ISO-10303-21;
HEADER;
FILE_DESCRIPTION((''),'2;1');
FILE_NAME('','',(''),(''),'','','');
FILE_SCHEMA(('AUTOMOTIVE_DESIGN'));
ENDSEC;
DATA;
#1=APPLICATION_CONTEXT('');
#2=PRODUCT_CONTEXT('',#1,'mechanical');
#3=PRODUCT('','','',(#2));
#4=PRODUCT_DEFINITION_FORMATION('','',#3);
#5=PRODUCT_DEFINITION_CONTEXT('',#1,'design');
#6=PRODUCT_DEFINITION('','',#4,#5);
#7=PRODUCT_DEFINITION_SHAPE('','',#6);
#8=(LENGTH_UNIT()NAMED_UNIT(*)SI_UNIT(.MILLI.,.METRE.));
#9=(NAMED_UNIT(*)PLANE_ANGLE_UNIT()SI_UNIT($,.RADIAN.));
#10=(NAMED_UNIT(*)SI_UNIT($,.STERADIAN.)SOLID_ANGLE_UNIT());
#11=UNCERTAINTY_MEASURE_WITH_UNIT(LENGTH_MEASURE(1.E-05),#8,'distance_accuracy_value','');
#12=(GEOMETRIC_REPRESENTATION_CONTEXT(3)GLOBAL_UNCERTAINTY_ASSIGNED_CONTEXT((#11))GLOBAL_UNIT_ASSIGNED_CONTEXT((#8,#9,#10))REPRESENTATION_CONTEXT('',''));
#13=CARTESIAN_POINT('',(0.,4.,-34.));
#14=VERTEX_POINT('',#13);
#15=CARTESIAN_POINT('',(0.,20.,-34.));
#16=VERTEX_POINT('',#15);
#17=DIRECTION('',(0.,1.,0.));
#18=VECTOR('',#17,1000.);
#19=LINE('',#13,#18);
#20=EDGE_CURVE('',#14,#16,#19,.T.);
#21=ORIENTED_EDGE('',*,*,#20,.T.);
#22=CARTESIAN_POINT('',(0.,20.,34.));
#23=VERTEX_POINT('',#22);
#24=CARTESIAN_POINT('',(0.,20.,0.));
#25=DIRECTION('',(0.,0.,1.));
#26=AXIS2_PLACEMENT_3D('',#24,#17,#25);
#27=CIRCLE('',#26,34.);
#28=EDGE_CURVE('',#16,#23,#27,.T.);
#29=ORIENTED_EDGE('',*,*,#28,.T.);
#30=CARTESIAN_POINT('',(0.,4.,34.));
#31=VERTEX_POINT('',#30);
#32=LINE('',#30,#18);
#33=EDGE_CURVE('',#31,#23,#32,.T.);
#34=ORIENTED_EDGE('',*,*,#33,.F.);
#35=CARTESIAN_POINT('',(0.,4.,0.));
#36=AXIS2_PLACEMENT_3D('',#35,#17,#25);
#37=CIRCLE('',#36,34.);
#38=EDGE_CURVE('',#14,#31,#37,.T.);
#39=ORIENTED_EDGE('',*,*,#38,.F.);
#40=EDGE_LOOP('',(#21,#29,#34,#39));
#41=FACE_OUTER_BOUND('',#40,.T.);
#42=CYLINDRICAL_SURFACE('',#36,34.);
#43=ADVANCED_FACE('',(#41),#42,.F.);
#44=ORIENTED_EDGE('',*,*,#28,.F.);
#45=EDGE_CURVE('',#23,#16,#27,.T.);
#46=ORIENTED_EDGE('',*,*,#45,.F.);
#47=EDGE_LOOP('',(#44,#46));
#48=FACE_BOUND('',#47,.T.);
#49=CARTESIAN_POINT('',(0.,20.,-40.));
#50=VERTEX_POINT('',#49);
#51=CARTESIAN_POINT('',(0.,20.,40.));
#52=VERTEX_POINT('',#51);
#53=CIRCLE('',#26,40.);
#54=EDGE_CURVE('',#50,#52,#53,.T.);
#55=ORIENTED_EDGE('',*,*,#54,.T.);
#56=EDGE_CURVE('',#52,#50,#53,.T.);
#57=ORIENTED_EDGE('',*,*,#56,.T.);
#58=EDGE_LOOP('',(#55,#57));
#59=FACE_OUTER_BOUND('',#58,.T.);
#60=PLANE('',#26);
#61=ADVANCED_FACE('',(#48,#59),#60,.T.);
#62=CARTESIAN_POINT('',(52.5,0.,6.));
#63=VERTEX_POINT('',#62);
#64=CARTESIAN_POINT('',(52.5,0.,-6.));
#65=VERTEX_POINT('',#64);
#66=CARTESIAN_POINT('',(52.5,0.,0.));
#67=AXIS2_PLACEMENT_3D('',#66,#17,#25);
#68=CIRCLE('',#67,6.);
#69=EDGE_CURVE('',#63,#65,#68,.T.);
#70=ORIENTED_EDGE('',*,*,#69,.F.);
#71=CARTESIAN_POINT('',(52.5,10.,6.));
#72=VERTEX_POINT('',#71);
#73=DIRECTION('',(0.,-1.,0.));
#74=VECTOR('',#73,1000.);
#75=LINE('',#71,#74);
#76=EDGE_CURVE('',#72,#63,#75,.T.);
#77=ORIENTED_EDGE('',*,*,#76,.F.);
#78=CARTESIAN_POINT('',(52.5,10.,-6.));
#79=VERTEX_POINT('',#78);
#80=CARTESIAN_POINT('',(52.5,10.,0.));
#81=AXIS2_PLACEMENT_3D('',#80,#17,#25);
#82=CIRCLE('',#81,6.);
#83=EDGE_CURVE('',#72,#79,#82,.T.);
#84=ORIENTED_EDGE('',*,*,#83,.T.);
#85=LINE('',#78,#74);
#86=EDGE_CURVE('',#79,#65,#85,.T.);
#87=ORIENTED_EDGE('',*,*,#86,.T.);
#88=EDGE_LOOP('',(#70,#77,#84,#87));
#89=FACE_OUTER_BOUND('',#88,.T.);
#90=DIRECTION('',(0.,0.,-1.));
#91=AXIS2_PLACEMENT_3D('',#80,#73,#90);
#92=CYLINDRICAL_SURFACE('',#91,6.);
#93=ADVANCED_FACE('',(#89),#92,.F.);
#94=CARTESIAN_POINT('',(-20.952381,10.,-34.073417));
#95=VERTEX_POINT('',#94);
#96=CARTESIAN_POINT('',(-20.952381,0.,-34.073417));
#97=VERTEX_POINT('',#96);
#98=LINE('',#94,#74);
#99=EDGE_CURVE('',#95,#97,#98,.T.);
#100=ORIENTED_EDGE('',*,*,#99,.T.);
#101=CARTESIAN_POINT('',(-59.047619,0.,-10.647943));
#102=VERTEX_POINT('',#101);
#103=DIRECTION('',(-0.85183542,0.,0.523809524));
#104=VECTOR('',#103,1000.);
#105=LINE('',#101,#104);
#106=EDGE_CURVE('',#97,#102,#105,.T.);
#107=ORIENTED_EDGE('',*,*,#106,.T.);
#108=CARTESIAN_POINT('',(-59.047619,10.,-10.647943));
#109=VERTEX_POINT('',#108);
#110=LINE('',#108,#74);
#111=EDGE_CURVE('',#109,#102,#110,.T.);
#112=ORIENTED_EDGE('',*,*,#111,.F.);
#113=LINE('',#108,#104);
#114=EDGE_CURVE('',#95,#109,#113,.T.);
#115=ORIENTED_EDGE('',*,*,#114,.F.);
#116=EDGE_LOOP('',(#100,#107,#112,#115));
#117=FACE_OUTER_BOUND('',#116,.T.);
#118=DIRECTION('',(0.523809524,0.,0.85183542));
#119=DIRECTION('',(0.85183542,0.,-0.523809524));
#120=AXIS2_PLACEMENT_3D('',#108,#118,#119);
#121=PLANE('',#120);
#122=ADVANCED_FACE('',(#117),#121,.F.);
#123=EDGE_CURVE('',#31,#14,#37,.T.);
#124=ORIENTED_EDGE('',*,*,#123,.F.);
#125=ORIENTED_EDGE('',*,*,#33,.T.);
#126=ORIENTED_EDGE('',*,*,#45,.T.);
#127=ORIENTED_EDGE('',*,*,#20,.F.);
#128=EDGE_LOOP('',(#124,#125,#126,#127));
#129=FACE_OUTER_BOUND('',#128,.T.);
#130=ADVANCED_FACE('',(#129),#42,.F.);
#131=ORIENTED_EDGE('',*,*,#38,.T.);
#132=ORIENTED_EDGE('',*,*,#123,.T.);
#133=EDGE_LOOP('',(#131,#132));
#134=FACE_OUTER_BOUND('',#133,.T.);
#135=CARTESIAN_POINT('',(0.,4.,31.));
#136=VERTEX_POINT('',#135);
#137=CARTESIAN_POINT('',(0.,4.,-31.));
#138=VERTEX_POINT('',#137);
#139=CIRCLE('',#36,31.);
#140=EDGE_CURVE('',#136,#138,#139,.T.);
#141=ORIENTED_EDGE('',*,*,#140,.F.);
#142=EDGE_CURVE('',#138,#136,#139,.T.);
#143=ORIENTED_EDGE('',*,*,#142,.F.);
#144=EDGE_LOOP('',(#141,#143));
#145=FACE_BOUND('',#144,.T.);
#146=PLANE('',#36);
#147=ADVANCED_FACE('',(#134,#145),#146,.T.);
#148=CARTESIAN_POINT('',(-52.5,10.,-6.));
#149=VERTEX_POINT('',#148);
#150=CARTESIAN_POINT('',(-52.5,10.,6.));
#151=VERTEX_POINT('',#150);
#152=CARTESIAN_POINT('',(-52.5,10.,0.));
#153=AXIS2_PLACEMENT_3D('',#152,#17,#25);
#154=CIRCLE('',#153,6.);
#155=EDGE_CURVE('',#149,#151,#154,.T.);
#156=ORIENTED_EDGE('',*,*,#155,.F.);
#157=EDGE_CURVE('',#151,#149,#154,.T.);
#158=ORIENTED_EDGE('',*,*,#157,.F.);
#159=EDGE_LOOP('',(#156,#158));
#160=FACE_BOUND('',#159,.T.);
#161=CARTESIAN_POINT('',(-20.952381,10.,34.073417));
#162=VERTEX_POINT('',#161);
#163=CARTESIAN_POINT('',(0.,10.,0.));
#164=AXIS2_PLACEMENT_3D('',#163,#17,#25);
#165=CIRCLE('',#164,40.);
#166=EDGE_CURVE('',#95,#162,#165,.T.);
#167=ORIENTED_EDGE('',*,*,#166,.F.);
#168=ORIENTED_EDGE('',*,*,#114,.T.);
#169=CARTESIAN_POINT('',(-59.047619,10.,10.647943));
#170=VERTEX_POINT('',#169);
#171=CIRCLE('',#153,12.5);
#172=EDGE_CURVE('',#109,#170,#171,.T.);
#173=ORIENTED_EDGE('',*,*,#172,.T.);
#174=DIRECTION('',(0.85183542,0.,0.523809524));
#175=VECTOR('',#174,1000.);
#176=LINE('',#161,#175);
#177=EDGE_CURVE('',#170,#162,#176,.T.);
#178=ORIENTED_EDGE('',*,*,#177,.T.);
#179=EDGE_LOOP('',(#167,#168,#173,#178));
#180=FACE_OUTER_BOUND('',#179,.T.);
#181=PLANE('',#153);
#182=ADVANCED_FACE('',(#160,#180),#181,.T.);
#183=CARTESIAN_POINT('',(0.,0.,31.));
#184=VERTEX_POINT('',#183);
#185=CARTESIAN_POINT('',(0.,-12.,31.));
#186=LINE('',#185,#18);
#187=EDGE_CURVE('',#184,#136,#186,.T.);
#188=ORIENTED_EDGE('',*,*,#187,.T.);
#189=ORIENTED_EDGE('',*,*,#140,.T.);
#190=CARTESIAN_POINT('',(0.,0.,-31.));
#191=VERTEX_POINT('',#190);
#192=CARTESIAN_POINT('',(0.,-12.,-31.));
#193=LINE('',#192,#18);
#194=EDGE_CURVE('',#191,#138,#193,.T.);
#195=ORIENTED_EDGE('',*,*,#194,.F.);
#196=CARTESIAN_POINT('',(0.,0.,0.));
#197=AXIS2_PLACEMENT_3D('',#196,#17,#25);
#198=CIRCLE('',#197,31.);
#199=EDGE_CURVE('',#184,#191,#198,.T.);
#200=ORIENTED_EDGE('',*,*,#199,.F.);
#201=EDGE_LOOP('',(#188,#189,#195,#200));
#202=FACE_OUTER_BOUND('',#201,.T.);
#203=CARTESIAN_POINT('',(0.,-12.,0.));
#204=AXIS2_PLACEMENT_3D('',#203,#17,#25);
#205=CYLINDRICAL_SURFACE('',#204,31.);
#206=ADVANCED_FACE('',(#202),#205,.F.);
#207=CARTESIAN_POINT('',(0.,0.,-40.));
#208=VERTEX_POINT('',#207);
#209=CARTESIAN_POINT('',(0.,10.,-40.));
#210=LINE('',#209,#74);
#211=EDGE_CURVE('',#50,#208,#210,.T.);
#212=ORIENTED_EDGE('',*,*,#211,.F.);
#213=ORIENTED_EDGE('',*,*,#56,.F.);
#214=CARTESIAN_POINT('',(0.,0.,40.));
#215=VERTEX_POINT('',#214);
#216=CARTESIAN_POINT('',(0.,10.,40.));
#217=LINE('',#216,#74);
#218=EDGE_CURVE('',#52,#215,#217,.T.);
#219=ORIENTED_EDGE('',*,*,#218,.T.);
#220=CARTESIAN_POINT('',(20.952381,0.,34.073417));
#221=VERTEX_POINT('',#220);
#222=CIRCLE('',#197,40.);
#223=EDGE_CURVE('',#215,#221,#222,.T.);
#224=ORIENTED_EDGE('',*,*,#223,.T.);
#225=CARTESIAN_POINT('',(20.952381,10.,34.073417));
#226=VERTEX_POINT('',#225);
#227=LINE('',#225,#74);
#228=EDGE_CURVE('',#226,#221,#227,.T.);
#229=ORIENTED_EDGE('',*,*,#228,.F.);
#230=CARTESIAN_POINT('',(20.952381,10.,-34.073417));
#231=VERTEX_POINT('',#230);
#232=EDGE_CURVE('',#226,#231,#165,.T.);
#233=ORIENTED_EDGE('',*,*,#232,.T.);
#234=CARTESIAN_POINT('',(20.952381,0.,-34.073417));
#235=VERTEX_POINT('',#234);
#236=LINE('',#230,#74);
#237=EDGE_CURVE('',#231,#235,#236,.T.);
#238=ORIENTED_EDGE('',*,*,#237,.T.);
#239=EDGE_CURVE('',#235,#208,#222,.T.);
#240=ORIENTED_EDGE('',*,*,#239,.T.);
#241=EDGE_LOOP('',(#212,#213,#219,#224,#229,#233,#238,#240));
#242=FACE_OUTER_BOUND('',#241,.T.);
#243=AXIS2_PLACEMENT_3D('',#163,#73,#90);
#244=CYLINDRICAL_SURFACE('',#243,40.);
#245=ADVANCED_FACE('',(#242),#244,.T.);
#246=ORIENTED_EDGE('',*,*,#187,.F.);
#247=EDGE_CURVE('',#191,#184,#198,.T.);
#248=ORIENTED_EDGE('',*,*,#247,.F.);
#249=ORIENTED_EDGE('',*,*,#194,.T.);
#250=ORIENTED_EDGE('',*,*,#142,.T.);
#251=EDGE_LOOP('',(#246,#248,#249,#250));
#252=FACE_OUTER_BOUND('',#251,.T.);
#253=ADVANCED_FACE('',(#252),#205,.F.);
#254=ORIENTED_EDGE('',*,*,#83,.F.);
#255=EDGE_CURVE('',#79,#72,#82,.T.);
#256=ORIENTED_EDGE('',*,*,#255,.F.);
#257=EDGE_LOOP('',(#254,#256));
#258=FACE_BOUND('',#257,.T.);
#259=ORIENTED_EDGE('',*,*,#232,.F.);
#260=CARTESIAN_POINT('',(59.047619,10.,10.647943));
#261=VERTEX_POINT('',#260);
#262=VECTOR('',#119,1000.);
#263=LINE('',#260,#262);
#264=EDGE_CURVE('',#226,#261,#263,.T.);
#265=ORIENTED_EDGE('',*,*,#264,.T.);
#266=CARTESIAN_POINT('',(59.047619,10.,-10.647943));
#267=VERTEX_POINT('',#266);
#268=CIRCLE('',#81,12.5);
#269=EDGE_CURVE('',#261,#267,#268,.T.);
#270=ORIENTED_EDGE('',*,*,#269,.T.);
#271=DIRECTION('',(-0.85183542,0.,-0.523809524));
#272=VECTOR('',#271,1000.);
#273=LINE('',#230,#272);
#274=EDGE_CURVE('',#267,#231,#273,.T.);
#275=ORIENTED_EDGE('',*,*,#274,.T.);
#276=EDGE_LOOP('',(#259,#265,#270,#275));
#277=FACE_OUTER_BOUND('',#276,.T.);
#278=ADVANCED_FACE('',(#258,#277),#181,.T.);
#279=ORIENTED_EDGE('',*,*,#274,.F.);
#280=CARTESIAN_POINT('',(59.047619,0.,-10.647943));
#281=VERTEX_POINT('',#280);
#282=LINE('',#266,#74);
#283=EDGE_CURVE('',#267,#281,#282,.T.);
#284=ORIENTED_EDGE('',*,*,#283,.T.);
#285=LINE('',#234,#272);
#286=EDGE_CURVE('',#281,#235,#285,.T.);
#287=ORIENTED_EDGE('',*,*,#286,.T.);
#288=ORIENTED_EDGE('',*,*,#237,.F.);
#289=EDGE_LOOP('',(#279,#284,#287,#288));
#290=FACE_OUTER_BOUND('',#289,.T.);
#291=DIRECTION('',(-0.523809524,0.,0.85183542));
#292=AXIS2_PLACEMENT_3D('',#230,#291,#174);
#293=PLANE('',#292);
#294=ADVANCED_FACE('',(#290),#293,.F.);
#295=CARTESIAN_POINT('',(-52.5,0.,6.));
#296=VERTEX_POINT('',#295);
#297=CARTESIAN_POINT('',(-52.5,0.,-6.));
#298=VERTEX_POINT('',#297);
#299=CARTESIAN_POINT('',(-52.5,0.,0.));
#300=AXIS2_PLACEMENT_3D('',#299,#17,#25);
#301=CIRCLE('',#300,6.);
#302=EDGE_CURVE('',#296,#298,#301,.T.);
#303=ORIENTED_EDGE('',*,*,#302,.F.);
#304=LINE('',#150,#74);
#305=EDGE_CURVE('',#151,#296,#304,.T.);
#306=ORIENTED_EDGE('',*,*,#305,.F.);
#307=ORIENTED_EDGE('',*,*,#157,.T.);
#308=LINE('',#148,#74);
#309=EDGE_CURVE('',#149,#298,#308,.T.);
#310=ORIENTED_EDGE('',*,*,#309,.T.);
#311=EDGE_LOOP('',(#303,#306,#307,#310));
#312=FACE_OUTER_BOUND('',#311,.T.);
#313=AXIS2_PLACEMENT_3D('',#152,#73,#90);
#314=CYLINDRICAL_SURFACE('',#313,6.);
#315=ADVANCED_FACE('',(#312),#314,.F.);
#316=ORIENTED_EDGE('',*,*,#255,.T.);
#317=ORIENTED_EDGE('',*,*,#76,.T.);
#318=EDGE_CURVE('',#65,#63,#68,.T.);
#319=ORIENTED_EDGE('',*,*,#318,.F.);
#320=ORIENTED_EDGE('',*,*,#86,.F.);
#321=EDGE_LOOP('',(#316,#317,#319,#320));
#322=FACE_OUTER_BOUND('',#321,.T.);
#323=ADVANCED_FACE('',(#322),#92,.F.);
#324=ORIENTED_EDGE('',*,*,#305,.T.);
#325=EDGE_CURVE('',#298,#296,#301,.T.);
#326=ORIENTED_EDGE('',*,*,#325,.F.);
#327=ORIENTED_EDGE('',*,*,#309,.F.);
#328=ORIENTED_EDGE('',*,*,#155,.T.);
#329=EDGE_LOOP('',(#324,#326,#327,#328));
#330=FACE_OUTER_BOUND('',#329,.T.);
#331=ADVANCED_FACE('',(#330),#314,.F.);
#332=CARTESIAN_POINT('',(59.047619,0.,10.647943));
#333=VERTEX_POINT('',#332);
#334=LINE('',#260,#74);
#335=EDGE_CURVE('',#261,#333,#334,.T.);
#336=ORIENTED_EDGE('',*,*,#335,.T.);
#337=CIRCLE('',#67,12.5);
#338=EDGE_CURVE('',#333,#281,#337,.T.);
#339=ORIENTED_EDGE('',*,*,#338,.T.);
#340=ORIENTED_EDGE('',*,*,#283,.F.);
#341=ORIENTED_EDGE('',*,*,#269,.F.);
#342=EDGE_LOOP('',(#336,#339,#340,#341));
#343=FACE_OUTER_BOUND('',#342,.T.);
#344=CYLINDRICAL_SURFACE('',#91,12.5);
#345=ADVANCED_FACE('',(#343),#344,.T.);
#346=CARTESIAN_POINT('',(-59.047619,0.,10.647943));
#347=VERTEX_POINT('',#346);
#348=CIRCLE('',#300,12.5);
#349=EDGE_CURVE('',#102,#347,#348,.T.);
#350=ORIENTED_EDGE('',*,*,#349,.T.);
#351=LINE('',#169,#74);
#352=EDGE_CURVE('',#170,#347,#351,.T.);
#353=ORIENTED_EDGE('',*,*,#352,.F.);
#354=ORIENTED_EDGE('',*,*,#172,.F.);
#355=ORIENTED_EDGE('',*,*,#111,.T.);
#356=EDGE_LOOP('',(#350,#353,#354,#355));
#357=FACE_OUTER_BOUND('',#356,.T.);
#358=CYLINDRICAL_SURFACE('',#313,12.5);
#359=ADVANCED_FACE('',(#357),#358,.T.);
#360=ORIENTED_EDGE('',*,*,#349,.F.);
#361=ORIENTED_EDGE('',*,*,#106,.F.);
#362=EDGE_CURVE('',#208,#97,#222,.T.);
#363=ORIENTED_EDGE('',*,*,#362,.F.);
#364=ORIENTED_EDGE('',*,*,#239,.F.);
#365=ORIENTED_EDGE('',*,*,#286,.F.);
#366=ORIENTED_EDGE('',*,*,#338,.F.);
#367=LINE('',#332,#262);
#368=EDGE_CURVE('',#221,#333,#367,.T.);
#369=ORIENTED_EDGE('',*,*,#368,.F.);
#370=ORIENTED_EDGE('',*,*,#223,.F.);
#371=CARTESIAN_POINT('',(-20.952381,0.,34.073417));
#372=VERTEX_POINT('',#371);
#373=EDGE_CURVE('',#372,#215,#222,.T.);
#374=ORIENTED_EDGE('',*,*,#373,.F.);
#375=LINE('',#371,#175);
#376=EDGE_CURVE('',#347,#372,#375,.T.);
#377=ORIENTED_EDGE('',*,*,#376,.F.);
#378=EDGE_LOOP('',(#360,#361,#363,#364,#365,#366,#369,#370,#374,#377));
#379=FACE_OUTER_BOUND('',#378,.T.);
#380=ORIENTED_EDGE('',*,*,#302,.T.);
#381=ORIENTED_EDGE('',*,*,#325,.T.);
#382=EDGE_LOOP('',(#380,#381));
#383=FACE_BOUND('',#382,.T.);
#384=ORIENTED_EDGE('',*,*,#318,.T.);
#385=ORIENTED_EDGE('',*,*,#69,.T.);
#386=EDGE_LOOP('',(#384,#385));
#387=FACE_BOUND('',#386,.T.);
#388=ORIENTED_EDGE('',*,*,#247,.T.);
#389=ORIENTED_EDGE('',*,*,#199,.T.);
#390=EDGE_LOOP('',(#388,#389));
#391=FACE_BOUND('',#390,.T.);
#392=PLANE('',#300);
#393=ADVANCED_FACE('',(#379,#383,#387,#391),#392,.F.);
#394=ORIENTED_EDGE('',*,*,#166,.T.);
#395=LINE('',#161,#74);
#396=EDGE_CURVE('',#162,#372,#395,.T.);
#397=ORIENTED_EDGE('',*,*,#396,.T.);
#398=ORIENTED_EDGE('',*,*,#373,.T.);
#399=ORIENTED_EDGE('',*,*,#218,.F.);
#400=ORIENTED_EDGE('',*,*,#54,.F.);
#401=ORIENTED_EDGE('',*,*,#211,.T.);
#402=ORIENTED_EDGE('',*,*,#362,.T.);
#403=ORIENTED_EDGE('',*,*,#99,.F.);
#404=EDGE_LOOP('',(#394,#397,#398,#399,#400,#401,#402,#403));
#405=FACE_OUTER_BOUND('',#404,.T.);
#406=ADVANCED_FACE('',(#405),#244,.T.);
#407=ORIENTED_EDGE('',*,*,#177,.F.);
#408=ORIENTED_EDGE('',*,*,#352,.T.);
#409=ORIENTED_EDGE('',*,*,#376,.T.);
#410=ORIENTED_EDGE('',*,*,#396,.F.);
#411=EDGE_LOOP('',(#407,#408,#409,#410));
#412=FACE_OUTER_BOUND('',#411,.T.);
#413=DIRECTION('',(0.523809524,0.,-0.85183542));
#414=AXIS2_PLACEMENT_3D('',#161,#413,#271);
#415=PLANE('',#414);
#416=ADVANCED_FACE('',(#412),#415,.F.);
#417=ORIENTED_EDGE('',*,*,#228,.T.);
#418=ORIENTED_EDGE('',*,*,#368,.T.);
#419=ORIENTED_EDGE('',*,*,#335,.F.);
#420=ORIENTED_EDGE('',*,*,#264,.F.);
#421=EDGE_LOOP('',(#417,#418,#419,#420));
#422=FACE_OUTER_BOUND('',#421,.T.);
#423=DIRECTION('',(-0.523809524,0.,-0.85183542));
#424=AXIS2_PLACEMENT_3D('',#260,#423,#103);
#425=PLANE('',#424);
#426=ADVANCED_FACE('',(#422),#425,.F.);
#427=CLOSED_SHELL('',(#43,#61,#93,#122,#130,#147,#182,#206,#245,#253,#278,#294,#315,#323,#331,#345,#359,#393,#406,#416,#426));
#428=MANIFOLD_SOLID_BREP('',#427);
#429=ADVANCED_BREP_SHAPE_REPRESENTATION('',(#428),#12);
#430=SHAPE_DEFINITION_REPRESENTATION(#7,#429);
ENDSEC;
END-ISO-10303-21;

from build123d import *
from build123d.topology import SkipClean

# Parameters (mm, degrees)
SKETCH_1_R          = 6
EXTRUDE_1_DEPTH     = 10
SKETCH_2_R          = 40
EXTRUDE_2_DEPTH     = 10
SKETCH_3_R          = 34
CUT_EXTRUDE_1_DEPTH = 16
SKETCH_4_R          = 31
CUT_EXTRUDE_2_DEPTH = 16


with BuildPart() as part:
    # 草图1 → 凸台-拉伸1 (new body)
    with BuildSketch(Plane(origin=(0, 0, 0), x_dir=(1, 0, 0), z_dir=(0, 1, 0))):
        with BuildLine():
            Line((-59.047619048, 10.64794275), (-20.952380952, 34.0734168))
            ThreePointArc((-20.952380952, 34.0734168), (0, 40), (20.952380952, 34.0734168))
            Line((20.952380952, 34.0734168), (59.047619048, 10.64794275))
            ThreePointArc((59.047619048, 10.64794275), (65, 0), (59.047619048, -10.64794275))
            Line((59.047619048, -10.64794275), (20.952380952, -34.0734168))
            ThreePointArc((20.952380952, -34.0734168), (0, -40), (-20.952380952, -34.0734168))
            Line((-20.952380952, -34.0734168), (-59.047619048, -10.64794275))
            ThreePointArc((-59.047619048, -10.64794275), (-65, 0), (-59.047619048, 10.64794275))
        make_face()
        with Locations(Location((52.5, 0, 0), (0, 0, 270))):
            Circle(SKETCH_1_R, mode=Mode.SUBTRACT)
        with Locations(Location((-52.5, 0, 0), (0, 0, 270))):
            Circle(SKETCH_1_R, mode=Mode.SUBTRACT)
    extrude(amount=EXTRUDE_1_DEPTH)

    # 草图2 → 凸台-拉伸2 (add)
    with SkipClean():  # the faces are left unmerged after this step: merging them gives an invalid solid
        with BuildSketch(Plane(origin=(0, 10, 0), x_dir=(1, 0, 0), z_dir=(0, 1, 0))):
            with Locations(Location((0, 0, 0), (0, 0, 121.588135505))):
                Circle(SKETCH_2_R)
        extrude(amount=EXTRUDE_2_DEPTH)

    # 草图3 → 切除-拉伸1 (cut)
    with SkipClean():  # the faces are left unmerged after this step: merging them gives an invalid solid
        with BuildSketch(Plane(origin=(0, 20, 0), x_dir=(1, 0, 0), z_dir=(0, 1, 0))):
            with Locations(Location((0, 0, 0), (0, 0, 270))):
                Circle(SKETCH_3_R)
        extrude(amount=-CUT_EXTRUDE_1_DEPTH, mode=Mode.SUBTRACT)

    # 草图4 → 切除-拉伸2 (cut)
    with SkipClean():  # the faces are left unmerged after this step: merging them gives an invalid solid
        with BuildSketch(Plane(origin=(0, 4, 0), x_dir=(1, 0, 0), z_dir=(0, 1, 0))):
            with Locations(Location((0, 0, 0), (0, 0, 270))):
                Circle(SKETCH_4_R)
        extrude(amount=-CUT_EXTRUDE_2_DEPTH, mode=Mode.SUBTRACT)


solid = part.part
